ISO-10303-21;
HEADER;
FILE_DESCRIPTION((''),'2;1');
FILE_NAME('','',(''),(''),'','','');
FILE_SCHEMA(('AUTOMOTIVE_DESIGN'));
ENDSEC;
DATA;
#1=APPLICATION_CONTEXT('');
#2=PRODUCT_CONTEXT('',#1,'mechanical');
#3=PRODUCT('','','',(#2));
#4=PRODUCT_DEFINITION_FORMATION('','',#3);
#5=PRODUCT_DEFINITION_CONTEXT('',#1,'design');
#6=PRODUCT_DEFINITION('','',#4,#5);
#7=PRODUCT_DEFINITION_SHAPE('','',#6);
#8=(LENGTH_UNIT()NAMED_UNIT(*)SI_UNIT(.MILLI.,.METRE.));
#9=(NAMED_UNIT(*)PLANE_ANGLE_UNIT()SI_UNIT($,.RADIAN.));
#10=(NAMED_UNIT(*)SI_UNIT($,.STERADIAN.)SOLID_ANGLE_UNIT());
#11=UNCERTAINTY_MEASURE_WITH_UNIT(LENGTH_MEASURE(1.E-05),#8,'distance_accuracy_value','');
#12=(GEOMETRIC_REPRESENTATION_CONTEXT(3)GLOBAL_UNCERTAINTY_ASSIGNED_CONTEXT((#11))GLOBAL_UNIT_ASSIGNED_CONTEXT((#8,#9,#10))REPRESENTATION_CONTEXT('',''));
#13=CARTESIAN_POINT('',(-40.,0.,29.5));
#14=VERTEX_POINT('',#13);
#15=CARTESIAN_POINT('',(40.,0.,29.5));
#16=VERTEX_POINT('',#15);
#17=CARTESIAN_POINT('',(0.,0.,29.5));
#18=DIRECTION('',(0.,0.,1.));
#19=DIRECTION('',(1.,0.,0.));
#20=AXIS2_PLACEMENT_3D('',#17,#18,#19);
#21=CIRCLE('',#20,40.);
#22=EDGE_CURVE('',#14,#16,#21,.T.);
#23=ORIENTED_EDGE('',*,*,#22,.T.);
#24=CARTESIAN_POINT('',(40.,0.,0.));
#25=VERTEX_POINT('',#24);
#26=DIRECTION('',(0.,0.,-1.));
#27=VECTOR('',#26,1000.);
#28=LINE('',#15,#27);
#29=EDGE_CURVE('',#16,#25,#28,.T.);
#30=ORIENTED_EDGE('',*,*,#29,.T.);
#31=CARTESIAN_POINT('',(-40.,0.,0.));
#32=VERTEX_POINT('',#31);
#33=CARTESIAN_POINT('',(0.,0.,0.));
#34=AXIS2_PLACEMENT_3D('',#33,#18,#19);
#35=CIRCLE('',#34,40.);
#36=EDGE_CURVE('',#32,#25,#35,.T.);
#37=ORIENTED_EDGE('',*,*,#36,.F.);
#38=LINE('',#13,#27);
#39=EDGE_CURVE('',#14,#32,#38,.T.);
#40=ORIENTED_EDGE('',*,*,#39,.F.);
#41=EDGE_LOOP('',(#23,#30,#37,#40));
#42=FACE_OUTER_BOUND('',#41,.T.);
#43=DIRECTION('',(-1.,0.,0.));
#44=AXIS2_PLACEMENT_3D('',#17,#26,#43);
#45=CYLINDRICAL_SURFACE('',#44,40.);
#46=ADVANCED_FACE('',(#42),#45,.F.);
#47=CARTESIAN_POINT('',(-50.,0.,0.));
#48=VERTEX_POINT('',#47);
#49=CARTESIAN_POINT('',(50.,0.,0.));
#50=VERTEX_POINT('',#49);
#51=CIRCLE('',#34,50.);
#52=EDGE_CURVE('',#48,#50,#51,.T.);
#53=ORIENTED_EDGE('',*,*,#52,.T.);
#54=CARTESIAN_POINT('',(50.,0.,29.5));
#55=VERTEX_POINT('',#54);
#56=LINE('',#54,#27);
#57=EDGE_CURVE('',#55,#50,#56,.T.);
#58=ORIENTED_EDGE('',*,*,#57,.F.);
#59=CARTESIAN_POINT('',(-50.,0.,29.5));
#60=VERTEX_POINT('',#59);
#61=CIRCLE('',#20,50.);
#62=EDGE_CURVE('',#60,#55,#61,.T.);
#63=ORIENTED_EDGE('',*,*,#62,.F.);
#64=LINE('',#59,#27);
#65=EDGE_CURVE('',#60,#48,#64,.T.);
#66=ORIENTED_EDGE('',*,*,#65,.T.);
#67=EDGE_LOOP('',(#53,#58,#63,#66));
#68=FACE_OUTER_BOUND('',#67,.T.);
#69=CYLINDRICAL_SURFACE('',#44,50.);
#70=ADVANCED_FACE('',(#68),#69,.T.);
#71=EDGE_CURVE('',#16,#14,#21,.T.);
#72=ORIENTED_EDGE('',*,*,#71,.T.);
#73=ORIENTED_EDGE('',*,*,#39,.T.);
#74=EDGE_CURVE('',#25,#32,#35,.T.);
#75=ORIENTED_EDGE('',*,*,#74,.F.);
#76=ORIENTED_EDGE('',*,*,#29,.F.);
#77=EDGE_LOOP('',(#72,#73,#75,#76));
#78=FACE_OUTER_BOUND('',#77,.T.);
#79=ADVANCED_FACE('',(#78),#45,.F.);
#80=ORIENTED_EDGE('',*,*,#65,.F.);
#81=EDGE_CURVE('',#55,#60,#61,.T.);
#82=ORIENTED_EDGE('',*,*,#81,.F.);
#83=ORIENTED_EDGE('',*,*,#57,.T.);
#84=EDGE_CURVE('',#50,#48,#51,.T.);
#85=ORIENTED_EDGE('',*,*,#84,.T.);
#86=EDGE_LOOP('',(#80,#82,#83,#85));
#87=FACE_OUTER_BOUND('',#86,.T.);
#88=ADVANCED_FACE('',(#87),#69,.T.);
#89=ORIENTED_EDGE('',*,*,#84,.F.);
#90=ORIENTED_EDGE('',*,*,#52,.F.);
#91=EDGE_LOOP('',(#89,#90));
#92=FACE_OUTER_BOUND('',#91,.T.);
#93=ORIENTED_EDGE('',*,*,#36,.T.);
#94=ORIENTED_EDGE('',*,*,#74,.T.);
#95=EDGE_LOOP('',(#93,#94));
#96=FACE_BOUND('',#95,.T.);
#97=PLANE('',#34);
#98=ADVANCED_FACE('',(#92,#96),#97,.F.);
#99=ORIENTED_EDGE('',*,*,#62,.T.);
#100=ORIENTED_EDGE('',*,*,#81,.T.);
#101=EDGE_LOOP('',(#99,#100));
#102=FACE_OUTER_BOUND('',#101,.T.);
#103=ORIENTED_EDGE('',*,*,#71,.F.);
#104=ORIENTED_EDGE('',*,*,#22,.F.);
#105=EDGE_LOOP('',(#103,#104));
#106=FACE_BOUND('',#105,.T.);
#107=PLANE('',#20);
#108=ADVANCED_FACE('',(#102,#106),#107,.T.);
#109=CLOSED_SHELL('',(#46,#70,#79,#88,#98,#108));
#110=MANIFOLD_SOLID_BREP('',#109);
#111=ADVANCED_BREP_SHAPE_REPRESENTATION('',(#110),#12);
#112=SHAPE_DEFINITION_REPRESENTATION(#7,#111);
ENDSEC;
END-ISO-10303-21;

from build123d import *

# Parameters (mm, degrees)
SKETCH1_R           = 50
SKETCH1_R_2         = 40
BOSS_EXTRUDE1_DEPTH = 29.5


with BuildPart() as part:
    # Sketch1 → Boss-Extrude1 (new body)
    with BuildSketch(Plane.XY):
        Circle(SKETCH1_R)
        Circle(SKETCH1_R_2, mode=Mode.SUBTRACT)
    extrude(amount=BOSS_EXTRUDE1_DEPTH)


solid = part.part
